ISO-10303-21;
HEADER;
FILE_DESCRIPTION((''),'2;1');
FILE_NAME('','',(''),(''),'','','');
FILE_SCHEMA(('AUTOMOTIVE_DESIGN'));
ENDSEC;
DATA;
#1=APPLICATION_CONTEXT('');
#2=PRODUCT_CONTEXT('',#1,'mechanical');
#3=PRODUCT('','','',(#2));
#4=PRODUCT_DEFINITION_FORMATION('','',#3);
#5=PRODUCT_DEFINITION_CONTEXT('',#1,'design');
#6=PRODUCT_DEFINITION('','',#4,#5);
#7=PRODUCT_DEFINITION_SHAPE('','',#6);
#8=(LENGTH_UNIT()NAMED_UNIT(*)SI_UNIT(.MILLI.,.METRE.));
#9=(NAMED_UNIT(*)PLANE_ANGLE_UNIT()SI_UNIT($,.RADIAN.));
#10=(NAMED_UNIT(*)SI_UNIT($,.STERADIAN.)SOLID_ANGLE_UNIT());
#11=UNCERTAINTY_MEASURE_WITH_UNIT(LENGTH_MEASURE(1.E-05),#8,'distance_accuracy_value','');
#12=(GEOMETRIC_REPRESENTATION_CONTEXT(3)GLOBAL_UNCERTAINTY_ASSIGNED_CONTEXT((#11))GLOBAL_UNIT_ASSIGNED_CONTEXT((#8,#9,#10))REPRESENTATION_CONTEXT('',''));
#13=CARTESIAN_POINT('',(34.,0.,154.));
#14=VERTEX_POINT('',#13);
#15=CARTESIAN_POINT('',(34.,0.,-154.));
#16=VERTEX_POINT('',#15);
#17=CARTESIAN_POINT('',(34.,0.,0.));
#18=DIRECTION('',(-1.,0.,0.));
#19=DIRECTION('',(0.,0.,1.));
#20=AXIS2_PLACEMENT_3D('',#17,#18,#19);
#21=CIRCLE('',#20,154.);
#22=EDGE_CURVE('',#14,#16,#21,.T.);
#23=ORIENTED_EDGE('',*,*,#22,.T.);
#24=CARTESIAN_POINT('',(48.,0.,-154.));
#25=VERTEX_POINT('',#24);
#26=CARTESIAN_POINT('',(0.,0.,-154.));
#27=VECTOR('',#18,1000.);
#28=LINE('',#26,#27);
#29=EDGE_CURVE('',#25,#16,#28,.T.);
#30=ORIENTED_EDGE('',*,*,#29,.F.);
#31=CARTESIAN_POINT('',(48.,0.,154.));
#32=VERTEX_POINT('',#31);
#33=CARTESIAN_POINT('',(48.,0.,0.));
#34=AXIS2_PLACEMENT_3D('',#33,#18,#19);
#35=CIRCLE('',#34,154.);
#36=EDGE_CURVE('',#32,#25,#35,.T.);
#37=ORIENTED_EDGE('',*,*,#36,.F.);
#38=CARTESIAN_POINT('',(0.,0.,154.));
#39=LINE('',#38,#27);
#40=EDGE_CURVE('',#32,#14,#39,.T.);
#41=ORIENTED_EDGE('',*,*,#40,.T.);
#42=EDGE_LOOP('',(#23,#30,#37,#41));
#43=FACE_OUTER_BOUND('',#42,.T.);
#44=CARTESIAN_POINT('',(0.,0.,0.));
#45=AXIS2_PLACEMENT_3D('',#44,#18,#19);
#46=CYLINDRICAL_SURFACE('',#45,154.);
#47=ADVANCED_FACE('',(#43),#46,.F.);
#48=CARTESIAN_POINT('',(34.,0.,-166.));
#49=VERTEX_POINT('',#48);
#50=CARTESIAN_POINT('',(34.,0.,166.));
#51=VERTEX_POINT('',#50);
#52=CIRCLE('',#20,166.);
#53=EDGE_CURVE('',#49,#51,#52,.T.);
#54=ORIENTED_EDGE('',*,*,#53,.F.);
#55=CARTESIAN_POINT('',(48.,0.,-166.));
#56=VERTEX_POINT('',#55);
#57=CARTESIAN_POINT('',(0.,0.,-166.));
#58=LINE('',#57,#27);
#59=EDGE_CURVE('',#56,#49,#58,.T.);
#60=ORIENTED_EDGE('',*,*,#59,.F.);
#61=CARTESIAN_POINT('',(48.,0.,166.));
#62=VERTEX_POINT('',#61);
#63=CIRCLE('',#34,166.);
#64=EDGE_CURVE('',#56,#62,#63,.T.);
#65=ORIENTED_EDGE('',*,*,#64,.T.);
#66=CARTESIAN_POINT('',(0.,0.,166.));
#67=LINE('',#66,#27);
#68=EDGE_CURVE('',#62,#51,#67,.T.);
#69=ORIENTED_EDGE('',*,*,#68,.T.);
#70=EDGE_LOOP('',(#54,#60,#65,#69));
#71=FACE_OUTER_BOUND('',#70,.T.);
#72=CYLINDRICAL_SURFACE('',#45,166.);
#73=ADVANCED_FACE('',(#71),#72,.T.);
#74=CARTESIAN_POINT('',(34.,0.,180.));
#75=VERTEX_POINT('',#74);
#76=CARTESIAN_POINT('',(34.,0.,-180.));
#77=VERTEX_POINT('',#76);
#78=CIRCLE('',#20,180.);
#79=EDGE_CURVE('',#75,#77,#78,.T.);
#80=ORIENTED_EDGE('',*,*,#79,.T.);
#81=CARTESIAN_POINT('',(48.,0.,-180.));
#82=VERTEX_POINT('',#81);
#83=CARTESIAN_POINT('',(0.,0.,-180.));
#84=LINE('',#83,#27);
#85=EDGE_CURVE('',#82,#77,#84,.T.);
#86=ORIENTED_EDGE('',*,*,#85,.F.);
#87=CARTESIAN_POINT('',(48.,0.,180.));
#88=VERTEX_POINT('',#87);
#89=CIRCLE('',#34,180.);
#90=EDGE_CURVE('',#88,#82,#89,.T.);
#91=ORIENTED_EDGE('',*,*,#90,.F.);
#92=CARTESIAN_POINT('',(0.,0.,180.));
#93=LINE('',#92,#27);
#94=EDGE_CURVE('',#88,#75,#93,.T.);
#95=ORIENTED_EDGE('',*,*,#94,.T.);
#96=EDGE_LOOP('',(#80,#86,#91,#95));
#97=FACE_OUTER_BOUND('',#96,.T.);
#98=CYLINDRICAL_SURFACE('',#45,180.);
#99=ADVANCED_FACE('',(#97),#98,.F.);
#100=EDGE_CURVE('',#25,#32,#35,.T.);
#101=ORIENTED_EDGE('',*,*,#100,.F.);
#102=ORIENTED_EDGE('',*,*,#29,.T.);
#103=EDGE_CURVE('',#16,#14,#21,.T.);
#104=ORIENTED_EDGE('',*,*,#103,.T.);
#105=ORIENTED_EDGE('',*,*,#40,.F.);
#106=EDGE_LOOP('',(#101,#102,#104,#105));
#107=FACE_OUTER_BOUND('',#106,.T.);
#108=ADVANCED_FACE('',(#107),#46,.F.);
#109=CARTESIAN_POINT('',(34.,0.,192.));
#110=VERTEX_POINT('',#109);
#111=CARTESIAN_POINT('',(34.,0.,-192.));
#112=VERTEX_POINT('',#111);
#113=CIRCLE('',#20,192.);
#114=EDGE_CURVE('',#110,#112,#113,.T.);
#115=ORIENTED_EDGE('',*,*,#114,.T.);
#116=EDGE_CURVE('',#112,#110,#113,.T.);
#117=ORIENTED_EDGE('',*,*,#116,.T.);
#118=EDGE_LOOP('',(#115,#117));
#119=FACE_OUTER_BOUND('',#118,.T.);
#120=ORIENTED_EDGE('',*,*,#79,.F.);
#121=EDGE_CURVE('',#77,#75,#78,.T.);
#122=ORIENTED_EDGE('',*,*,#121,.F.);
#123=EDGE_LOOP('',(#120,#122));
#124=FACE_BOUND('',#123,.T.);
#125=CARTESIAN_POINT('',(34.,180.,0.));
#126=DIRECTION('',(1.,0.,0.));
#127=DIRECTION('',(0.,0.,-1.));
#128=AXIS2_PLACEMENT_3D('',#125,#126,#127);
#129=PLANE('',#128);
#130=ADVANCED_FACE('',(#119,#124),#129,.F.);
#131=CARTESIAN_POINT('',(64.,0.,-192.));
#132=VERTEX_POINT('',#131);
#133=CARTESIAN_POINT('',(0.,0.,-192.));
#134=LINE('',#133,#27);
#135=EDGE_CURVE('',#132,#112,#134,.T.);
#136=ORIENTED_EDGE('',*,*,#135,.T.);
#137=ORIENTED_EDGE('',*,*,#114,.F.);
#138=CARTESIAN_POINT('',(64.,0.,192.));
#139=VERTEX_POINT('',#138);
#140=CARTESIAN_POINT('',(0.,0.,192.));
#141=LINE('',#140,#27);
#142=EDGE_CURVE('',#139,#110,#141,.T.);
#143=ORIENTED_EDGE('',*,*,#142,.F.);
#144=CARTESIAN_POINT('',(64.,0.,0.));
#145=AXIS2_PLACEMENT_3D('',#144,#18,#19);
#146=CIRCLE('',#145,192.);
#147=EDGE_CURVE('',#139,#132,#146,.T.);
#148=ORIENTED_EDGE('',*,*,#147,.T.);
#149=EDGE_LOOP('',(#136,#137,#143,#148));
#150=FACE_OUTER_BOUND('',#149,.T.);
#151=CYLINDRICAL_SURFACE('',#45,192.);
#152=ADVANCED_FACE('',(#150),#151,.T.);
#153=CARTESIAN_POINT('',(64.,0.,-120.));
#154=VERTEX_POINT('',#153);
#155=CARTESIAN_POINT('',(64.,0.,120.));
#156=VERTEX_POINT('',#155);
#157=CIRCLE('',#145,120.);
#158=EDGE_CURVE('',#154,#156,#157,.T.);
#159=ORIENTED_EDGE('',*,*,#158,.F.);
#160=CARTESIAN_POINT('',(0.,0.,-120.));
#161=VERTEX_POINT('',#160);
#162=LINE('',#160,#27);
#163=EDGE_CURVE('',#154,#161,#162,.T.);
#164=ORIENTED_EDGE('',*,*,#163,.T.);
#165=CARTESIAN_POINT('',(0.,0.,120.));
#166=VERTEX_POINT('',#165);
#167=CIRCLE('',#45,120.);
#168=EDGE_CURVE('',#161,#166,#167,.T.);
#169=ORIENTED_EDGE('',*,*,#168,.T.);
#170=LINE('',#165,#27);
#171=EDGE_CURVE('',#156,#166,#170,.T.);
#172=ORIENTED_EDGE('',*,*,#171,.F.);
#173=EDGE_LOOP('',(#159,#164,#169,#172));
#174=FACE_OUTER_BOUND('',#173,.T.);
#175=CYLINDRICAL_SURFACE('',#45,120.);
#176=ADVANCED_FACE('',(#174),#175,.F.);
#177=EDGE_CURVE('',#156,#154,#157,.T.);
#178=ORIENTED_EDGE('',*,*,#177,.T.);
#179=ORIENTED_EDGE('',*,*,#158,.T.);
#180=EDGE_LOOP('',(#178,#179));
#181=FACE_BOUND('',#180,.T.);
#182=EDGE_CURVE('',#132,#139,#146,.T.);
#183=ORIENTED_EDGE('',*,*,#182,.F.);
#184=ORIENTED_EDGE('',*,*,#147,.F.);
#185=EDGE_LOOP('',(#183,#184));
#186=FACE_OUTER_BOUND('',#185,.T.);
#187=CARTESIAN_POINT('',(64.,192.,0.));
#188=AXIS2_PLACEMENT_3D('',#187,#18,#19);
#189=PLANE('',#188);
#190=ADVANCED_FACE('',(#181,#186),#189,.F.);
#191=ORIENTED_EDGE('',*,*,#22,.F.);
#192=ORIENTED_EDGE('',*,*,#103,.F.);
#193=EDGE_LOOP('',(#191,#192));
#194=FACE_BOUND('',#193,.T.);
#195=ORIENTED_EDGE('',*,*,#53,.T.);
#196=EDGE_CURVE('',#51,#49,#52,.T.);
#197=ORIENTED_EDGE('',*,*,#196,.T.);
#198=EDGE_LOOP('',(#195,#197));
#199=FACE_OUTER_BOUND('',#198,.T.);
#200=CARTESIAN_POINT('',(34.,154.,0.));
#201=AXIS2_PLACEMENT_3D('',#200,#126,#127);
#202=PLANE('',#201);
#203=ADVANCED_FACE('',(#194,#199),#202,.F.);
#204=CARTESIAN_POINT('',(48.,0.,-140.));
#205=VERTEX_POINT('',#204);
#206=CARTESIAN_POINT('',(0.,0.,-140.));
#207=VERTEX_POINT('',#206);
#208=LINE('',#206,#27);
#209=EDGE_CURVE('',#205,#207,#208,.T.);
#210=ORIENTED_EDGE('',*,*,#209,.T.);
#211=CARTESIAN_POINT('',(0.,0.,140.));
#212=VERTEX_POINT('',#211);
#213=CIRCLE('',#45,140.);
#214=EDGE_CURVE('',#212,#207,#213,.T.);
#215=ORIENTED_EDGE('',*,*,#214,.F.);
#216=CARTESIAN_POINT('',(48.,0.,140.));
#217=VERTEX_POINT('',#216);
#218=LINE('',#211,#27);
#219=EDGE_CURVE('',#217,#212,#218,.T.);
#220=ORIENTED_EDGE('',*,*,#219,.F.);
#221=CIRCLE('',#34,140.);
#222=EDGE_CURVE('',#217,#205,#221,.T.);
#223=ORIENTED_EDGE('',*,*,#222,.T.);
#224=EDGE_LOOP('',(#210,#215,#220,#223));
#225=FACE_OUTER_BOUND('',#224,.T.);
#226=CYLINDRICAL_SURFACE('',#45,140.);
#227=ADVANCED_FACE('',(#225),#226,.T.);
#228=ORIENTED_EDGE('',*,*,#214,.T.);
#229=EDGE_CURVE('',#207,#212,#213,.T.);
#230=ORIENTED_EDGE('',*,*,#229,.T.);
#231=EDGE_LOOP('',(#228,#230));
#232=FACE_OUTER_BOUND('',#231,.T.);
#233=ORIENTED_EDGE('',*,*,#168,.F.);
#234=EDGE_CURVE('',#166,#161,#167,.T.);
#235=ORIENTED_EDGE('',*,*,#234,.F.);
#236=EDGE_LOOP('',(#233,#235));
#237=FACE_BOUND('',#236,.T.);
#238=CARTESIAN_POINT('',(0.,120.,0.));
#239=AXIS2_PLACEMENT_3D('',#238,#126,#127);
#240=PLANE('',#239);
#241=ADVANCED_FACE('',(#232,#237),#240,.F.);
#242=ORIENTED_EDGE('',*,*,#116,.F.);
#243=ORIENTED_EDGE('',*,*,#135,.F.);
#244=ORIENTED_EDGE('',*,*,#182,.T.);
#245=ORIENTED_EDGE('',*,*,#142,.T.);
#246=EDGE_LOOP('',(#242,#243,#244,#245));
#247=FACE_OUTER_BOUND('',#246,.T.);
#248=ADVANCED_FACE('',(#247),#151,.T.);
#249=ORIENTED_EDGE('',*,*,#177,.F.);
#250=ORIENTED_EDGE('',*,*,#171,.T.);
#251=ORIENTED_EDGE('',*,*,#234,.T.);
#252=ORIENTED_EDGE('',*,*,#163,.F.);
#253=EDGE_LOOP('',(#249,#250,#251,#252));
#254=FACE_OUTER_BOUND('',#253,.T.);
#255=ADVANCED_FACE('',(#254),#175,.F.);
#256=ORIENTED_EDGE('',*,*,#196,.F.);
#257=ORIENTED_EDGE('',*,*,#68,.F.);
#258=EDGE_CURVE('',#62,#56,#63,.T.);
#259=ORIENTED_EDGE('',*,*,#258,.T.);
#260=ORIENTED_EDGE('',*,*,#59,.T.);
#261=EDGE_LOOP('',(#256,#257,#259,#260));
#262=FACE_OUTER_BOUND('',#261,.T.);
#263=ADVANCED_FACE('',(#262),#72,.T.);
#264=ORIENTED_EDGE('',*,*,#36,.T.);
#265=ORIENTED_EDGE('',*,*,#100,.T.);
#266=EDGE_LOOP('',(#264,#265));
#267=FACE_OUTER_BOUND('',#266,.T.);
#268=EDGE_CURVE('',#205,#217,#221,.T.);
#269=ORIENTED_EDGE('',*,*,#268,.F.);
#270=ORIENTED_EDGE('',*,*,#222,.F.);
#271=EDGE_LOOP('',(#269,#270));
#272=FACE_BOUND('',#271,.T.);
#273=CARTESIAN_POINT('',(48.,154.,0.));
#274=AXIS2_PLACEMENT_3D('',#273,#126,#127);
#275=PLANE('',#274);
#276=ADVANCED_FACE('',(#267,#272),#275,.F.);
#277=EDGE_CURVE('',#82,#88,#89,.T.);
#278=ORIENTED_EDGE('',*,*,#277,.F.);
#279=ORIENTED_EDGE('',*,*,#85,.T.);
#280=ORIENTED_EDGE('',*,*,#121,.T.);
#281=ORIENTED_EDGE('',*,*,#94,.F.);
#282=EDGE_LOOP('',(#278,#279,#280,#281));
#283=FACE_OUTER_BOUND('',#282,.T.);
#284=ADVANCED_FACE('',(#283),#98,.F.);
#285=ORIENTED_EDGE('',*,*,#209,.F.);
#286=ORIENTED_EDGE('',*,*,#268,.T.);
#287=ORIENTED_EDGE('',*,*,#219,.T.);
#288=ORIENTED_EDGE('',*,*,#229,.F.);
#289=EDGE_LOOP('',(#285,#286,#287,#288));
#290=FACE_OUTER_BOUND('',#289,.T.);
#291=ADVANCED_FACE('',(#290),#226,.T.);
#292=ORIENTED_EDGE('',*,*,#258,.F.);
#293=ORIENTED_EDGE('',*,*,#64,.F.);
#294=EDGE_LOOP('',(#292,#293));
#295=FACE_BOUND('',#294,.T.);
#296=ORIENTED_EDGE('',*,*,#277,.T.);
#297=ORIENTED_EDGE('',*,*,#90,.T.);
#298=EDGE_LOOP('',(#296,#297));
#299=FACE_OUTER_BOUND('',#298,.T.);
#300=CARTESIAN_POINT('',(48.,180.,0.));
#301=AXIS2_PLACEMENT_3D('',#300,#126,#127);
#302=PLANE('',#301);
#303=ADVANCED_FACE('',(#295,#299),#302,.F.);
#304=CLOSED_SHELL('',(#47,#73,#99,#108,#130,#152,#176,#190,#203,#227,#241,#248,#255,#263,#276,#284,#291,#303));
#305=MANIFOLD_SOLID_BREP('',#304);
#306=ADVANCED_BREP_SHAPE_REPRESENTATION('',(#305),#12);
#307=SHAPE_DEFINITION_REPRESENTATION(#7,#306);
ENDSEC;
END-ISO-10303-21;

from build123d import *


with BuildPart() as part:
    # Sketch1 → Revolve1 (revolve)
    with BuildSketch(Plane.XY, mode=Mode.PRIVATE) as revolve1_sk:
        Polygon((0, 120), (0, 140), (48, 140), (48, 154), (34, 154), (34, 166), (48, 166), (48, 180), (34, 180), (34, 192), (64, 192), (64, 120), align=None)
    revolve(revolve1_sk.sketch.rotate(Axis((0, 0, 0), (1, 0, 0)), 90), axis=Axis((0, 0, 0), (1, 0, 0)))


solid = part.part
